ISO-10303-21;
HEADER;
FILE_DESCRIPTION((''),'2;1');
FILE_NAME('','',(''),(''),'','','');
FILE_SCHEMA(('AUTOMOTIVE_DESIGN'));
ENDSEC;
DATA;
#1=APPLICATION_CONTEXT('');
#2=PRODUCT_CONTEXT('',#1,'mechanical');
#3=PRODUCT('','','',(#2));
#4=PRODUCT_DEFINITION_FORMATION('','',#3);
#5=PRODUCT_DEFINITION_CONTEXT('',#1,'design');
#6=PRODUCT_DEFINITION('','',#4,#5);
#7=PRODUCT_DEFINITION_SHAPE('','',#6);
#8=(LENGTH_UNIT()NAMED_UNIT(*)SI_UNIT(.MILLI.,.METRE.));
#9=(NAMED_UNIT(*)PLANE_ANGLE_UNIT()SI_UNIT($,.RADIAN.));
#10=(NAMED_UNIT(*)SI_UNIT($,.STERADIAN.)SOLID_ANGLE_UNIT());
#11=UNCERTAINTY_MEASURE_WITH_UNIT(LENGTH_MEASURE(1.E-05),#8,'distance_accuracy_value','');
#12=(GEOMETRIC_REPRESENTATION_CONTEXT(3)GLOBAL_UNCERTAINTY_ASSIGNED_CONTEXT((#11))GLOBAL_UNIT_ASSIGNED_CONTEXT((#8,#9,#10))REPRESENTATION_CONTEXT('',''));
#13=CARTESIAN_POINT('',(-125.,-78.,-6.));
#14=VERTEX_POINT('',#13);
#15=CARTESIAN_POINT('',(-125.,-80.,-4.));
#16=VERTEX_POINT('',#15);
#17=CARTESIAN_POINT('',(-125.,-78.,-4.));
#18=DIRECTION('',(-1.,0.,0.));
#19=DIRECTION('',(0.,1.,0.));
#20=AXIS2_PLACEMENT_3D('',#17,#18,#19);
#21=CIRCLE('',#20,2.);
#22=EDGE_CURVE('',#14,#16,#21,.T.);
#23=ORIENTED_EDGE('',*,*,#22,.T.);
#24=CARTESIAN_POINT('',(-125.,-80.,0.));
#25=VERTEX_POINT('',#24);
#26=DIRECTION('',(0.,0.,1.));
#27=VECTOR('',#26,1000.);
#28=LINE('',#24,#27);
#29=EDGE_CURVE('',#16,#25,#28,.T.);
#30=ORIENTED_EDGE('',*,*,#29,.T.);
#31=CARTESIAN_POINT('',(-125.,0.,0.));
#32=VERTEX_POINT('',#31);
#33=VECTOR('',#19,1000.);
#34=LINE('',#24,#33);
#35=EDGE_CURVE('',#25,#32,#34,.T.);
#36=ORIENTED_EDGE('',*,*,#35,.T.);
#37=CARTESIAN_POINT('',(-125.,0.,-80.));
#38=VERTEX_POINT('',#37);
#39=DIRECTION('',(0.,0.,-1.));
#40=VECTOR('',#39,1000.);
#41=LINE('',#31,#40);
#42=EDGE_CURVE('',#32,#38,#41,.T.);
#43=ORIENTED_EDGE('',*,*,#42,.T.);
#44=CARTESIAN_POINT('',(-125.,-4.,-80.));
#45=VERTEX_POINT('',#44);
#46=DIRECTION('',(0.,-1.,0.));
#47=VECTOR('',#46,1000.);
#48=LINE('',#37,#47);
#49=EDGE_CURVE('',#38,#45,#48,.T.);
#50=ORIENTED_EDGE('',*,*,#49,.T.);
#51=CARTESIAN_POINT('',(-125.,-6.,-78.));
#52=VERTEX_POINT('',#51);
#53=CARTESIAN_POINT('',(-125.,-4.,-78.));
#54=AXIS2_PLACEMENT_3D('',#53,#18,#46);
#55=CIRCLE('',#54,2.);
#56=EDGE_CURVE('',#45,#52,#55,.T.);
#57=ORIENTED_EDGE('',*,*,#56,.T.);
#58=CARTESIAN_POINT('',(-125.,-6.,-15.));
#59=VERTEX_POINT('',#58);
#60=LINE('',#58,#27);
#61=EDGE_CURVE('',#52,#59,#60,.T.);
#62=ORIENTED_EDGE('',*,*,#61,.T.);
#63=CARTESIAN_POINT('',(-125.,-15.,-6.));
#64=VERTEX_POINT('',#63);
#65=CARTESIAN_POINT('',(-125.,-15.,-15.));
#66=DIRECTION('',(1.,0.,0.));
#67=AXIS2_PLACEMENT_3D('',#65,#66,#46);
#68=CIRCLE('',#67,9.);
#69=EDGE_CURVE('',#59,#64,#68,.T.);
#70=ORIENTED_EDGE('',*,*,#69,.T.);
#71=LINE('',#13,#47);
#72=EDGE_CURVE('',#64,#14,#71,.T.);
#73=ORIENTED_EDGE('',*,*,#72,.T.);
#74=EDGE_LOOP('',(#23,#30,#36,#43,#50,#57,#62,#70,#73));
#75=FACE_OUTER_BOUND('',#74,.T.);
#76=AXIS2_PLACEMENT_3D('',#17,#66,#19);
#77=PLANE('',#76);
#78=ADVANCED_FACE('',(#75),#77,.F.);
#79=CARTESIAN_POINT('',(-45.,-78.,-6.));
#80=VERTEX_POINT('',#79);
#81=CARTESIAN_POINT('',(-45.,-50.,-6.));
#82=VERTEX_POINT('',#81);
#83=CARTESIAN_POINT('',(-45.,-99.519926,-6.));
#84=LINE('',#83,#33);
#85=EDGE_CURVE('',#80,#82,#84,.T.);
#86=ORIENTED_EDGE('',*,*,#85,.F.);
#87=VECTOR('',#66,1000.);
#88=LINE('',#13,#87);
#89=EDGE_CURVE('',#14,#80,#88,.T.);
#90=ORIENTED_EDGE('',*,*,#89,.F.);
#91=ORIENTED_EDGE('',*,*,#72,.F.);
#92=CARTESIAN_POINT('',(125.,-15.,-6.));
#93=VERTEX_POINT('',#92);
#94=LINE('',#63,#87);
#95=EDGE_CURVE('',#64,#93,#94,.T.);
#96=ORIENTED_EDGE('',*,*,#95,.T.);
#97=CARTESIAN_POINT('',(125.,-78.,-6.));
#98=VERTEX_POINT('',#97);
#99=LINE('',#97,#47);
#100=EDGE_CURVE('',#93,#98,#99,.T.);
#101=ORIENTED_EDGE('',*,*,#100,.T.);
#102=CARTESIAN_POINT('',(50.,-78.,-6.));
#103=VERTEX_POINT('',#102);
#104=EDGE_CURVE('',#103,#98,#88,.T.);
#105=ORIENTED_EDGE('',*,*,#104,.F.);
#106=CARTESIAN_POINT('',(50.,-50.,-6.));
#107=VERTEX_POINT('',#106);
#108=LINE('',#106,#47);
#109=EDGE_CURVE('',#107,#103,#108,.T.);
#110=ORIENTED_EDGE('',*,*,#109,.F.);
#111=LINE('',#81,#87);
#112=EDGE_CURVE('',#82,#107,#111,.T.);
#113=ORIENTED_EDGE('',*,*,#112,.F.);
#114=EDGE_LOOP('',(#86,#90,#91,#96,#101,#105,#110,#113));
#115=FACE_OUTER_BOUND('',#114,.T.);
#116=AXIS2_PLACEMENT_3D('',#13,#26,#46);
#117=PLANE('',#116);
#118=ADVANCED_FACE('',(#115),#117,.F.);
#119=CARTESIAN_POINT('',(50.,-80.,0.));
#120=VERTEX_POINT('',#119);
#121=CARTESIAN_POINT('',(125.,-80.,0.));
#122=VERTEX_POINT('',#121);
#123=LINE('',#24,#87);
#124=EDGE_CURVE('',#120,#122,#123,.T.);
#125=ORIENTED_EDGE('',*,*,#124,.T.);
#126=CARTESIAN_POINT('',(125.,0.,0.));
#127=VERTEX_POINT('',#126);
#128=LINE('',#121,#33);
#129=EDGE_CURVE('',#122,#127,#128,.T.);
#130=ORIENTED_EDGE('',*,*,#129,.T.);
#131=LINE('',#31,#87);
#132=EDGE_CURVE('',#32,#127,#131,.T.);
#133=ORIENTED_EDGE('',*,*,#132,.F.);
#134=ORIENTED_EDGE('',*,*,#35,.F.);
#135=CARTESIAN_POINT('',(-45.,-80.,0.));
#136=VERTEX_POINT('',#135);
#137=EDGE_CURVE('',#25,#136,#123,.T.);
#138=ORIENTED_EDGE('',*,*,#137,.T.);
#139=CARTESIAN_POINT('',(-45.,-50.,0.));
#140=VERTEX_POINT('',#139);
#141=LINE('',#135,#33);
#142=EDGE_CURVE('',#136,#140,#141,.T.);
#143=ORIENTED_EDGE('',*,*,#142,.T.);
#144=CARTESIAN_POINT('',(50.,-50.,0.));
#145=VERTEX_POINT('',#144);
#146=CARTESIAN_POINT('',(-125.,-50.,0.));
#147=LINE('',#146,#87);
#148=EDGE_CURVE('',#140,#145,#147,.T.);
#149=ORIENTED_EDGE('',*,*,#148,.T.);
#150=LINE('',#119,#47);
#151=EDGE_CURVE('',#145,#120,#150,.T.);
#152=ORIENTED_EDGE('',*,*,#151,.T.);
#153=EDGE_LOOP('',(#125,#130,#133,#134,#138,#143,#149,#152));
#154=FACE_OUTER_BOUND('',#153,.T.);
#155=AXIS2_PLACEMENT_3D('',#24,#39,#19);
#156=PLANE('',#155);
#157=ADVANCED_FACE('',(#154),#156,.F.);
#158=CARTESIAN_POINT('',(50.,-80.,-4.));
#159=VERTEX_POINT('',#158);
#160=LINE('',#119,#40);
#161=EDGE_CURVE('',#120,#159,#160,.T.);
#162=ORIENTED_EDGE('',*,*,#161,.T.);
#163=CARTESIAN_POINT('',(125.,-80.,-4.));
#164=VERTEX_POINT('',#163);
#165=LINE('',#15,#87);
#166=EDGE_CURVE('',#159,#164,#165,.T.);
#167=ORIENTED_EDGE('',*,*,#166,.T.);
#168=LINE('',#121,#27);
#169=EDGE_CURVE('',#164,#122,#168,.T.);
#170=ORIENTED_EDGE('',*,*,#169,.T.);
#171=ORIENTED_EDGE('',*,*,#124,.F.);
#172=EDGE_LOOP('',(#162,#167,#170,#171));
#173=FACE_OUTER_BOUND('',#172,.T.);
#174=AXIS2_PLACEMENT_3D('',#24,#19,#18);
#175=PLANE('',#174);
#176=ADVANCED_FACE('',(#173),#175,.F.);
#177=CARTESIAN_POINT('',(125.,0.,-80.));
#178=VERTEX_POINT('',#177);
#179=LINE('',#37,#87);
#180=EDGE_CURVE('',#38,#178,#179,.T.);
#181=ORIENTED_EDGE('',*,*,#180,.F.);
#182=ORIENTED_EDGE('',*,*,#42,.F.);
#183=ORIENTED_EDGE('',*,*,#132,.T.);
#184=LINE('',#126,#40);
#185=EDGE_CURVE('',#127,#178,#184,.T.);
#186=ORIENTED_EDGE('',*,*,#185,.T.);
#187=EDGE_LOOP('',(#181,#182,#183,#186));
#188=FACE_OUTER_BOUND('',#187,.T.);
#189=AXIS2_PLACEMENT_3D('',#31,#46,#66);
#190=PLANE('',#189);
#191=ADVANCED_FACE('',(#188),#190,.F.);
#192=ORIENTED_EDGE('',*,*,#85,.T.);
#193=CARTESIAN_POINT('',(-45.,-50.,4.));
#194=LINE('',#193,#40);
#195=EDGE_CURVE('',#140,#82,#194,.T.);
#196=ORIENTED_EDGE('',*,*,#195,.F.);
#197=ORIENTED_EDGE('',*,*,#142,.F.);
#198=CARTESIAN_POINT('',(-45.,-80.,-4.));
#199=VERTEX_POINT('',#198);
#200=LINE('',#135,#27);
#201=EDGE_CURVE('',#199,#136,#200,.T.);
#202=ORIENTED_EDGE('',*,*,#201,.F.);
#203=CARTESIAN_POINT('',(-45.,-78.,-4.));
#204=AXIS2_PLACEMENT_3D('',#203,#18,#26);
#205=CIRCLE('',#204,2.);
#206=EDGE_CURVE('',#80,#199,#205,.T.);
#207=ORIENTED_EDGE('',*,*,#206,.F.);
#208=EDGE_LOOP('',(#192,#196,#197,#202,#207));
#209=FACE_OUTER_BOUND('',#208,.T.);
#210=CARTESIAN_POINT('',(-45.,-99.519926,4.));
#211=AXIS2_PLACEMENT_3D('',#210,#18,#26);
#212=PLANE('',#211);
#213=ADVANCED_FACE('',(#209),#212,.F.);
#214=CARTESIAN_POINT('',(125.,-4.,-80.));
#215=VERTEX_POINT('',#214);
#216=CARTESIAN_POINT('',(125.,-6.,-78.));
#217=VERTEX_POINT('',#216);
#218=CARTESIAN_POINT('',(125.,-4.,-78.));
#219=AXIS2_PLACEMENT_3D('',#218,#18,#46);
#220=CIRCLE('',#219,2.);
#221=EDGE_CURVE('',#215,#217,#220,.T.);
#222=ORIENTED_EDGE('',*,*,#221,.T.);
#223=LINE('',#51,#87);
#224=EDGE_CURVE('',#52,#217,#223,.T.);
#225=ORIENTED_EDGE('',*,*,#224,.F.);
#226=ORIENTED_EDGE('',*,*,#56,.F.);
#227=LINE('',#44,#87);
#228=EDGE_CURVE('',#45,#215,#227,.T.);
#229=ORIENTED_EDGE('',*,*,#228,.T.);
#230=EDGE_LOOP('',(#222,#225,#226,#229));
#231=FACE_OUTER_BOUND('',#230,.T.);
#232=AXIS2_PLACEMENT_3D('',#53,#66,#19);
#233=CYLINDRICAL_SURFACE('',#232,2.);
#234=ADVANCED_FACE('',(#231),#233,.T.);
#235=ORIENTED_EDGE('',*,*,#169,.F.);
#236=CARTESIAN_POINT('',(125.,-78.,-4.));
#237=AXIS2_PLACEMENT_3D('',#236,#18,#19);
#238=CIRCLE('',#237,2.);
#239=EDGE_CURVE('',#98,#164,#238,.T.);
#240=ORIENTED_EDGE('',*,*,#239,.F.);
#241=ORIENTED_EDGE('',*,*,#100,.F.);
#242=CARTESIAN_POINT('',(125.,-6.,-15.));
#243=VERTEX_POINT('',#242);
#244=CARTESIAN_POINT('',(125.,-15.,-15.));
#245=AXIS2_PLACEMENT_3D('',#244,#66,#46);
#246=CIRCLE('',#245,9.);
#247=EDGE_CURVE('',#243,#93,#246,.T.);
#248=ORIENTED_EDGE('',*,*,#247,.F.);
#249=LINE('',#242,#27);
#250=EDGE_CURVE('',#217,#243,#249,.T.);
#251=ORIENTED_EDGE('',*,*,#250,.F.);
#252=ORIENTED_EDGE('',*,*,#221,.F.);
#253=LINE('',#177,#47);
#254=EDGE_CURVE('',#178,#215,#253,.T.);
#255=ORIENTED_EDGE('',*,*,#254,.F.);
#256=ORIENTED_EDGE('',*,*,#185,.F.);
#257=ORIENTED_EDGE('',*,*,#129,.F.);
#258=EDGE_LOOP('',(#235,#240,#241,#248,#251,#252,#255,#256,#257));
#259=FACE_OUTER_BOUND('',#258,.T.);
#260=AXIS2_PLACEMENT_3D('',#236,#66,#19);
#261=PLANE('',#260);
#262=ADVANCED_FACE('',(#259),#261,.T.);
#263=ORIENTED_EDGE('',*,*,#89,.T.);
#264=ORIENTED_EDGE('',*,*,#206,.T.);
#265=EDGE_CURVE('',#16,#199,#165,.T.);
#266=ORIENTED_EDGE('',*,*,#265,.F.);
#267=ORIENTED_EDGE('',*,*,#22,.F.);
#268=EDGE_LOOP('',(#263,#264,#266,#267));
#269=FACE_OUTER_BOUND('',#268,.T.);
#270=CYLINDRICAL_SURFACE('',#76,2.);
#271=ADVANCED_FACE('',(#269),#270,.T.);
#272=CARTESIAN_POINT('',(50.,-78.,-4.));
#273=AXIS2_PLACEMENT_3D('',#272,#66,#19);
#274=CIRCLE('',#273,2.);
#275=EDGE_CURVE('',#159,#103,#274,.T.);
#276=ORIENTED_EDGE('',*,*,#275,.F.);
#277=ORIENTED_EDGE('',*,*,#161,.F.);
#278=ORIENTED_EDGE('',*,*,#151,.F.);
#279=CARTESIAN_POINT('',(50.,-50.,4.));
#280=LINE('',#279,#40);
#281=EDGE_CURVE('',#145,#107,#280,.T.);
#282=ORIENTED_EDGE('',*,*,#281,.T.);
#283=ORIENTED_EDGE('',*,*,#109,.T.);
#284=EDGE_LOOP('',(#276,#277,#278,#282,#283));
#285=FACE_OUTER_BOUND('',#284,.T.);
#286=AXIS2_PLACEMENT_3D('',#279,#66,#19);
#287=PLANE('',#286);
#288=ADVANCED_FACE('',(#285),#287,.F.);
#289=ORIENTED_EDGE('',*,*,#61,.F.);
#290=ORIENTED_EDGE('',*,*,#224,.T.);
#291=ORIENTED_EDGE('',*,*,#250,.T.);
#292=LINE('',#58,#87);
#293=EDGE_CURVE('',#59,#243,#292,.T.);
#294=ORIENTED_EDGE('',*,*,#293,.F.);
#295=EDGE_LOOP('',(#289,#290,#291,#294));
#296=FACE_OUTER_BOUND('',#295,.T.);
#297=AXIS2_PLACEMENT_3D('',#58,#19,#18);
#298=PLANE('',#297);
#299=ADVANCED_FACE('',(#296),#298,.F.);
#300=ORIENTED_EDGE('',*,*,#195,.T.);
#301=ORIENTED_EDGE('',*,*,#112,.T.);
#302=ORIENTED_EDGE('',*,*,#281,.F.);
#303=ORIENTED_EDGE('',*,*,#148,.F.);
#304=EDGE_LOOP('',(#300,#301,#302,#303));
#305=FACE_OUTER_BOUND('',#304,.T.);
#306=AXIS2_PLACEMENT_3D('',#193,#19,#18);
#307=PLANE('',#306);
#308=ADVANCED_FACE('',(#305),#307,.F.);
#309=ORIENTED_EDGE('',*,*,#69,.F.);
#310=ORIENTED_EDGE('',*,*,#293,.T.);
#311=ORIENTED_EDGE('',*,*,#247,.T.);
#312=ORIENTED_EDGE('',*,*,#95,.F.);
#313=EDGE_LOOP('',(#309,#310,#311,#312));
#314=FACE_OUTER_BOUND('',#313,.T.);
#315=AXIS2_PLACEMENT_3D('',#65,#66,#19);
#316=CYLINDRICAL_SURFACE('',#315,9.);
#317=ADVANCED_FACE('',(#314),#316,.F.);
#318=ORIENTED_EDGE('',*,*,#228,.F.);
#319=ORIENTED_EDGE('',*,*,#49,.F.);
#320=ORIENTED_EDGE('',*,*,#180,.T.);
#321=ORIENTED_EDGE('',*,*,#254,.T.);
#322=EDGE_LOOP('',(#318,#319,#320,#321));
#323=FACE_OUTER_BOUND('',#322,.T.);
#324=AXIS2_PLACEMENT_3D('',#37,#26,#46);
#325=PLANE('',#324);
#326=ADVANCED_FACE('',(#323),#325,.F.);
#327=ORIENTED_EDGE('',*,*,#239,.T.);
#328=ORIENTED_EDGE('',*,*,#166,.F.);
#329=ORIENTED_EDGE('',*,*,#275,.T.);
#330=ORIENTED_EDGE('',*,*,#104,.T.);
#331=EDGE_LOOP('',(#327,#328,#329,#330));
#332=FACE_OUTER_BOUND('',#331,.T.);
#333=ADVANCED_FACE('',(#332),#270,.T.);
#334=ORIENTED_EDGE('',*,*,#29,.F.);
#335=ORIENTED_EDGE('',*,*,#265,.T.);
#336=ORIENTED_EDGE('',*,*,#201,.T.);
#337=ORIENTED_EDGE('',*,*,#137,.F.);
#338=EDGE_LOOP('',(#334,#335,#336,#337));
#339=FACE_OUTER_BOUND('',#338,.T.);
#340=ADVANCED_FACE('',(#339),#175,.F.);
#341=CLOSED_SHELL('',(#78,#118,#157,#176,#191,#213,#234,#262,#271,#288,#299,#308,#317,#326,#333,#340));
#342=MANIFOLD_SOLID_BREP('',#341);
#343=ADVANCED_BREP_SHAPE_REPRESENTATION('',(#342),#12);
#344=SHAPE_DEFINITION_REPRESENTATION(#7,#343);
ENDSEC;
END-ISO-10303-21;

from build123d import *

# Parameters (mm, degrees)
HOT_ROLLED_EQUAL_ANGLE_STEEL_GB_T_9787_DEPTH = 250
SKETCH3_W                                    = 95
SKETCH3_H                                    = 49.519926073
CUT_EXTRUDE1_DEPTH                           = 10


with BuildPart() as part:
    # Sketch1 → hot-rolled equal angle steel (GB/T 9787-1988) 80×6(1) (new body)
    with BuildSketch(Plane(origin=(125, 0, 0), x_dir=(0, -1, 0), z_dir=(-1, 0, 0))):
        with BuildLine():
            Line((80, 0), (0, 0))
            Line((0, 0), (0, -80))
            Line((0, -80), (4, -80))
            ThreePointArc((4, -80), (5.414213562, -79.414213562), (6, -78))
            Line((6, -78), (6, -15))
            ThreePointArc((6, -15), (8.636038969, -8.636038969), (15, -6))
            Line((15, -6), (78, -6))
            ThreePointArc((78, -6), (79.414213562, -5.414213562), (80, -4))
            Line((80, -4), (80, 0))
        make_face()
    extrude(amount=HOT_ROLLED_EQUAL_ANGLE_STEEL_GB_T_9787_DEPTH)

    # Sketch3 → Cut-Extrude1 (cut)
    with BuildSketch(Plane(origin=(0, 0, -6), x_dir=(-1, 0, 0), z_dir=(0, 0, -1))):
        with Locations((-2.5, -74.759963037)):
            Rectangle(SKETCH3_W, SKETCH3_H)
    extrude(amount=-CUT_EXTRUDE1_DEPTH, mode=Mode.SUBTRACT)


solid = part.part
